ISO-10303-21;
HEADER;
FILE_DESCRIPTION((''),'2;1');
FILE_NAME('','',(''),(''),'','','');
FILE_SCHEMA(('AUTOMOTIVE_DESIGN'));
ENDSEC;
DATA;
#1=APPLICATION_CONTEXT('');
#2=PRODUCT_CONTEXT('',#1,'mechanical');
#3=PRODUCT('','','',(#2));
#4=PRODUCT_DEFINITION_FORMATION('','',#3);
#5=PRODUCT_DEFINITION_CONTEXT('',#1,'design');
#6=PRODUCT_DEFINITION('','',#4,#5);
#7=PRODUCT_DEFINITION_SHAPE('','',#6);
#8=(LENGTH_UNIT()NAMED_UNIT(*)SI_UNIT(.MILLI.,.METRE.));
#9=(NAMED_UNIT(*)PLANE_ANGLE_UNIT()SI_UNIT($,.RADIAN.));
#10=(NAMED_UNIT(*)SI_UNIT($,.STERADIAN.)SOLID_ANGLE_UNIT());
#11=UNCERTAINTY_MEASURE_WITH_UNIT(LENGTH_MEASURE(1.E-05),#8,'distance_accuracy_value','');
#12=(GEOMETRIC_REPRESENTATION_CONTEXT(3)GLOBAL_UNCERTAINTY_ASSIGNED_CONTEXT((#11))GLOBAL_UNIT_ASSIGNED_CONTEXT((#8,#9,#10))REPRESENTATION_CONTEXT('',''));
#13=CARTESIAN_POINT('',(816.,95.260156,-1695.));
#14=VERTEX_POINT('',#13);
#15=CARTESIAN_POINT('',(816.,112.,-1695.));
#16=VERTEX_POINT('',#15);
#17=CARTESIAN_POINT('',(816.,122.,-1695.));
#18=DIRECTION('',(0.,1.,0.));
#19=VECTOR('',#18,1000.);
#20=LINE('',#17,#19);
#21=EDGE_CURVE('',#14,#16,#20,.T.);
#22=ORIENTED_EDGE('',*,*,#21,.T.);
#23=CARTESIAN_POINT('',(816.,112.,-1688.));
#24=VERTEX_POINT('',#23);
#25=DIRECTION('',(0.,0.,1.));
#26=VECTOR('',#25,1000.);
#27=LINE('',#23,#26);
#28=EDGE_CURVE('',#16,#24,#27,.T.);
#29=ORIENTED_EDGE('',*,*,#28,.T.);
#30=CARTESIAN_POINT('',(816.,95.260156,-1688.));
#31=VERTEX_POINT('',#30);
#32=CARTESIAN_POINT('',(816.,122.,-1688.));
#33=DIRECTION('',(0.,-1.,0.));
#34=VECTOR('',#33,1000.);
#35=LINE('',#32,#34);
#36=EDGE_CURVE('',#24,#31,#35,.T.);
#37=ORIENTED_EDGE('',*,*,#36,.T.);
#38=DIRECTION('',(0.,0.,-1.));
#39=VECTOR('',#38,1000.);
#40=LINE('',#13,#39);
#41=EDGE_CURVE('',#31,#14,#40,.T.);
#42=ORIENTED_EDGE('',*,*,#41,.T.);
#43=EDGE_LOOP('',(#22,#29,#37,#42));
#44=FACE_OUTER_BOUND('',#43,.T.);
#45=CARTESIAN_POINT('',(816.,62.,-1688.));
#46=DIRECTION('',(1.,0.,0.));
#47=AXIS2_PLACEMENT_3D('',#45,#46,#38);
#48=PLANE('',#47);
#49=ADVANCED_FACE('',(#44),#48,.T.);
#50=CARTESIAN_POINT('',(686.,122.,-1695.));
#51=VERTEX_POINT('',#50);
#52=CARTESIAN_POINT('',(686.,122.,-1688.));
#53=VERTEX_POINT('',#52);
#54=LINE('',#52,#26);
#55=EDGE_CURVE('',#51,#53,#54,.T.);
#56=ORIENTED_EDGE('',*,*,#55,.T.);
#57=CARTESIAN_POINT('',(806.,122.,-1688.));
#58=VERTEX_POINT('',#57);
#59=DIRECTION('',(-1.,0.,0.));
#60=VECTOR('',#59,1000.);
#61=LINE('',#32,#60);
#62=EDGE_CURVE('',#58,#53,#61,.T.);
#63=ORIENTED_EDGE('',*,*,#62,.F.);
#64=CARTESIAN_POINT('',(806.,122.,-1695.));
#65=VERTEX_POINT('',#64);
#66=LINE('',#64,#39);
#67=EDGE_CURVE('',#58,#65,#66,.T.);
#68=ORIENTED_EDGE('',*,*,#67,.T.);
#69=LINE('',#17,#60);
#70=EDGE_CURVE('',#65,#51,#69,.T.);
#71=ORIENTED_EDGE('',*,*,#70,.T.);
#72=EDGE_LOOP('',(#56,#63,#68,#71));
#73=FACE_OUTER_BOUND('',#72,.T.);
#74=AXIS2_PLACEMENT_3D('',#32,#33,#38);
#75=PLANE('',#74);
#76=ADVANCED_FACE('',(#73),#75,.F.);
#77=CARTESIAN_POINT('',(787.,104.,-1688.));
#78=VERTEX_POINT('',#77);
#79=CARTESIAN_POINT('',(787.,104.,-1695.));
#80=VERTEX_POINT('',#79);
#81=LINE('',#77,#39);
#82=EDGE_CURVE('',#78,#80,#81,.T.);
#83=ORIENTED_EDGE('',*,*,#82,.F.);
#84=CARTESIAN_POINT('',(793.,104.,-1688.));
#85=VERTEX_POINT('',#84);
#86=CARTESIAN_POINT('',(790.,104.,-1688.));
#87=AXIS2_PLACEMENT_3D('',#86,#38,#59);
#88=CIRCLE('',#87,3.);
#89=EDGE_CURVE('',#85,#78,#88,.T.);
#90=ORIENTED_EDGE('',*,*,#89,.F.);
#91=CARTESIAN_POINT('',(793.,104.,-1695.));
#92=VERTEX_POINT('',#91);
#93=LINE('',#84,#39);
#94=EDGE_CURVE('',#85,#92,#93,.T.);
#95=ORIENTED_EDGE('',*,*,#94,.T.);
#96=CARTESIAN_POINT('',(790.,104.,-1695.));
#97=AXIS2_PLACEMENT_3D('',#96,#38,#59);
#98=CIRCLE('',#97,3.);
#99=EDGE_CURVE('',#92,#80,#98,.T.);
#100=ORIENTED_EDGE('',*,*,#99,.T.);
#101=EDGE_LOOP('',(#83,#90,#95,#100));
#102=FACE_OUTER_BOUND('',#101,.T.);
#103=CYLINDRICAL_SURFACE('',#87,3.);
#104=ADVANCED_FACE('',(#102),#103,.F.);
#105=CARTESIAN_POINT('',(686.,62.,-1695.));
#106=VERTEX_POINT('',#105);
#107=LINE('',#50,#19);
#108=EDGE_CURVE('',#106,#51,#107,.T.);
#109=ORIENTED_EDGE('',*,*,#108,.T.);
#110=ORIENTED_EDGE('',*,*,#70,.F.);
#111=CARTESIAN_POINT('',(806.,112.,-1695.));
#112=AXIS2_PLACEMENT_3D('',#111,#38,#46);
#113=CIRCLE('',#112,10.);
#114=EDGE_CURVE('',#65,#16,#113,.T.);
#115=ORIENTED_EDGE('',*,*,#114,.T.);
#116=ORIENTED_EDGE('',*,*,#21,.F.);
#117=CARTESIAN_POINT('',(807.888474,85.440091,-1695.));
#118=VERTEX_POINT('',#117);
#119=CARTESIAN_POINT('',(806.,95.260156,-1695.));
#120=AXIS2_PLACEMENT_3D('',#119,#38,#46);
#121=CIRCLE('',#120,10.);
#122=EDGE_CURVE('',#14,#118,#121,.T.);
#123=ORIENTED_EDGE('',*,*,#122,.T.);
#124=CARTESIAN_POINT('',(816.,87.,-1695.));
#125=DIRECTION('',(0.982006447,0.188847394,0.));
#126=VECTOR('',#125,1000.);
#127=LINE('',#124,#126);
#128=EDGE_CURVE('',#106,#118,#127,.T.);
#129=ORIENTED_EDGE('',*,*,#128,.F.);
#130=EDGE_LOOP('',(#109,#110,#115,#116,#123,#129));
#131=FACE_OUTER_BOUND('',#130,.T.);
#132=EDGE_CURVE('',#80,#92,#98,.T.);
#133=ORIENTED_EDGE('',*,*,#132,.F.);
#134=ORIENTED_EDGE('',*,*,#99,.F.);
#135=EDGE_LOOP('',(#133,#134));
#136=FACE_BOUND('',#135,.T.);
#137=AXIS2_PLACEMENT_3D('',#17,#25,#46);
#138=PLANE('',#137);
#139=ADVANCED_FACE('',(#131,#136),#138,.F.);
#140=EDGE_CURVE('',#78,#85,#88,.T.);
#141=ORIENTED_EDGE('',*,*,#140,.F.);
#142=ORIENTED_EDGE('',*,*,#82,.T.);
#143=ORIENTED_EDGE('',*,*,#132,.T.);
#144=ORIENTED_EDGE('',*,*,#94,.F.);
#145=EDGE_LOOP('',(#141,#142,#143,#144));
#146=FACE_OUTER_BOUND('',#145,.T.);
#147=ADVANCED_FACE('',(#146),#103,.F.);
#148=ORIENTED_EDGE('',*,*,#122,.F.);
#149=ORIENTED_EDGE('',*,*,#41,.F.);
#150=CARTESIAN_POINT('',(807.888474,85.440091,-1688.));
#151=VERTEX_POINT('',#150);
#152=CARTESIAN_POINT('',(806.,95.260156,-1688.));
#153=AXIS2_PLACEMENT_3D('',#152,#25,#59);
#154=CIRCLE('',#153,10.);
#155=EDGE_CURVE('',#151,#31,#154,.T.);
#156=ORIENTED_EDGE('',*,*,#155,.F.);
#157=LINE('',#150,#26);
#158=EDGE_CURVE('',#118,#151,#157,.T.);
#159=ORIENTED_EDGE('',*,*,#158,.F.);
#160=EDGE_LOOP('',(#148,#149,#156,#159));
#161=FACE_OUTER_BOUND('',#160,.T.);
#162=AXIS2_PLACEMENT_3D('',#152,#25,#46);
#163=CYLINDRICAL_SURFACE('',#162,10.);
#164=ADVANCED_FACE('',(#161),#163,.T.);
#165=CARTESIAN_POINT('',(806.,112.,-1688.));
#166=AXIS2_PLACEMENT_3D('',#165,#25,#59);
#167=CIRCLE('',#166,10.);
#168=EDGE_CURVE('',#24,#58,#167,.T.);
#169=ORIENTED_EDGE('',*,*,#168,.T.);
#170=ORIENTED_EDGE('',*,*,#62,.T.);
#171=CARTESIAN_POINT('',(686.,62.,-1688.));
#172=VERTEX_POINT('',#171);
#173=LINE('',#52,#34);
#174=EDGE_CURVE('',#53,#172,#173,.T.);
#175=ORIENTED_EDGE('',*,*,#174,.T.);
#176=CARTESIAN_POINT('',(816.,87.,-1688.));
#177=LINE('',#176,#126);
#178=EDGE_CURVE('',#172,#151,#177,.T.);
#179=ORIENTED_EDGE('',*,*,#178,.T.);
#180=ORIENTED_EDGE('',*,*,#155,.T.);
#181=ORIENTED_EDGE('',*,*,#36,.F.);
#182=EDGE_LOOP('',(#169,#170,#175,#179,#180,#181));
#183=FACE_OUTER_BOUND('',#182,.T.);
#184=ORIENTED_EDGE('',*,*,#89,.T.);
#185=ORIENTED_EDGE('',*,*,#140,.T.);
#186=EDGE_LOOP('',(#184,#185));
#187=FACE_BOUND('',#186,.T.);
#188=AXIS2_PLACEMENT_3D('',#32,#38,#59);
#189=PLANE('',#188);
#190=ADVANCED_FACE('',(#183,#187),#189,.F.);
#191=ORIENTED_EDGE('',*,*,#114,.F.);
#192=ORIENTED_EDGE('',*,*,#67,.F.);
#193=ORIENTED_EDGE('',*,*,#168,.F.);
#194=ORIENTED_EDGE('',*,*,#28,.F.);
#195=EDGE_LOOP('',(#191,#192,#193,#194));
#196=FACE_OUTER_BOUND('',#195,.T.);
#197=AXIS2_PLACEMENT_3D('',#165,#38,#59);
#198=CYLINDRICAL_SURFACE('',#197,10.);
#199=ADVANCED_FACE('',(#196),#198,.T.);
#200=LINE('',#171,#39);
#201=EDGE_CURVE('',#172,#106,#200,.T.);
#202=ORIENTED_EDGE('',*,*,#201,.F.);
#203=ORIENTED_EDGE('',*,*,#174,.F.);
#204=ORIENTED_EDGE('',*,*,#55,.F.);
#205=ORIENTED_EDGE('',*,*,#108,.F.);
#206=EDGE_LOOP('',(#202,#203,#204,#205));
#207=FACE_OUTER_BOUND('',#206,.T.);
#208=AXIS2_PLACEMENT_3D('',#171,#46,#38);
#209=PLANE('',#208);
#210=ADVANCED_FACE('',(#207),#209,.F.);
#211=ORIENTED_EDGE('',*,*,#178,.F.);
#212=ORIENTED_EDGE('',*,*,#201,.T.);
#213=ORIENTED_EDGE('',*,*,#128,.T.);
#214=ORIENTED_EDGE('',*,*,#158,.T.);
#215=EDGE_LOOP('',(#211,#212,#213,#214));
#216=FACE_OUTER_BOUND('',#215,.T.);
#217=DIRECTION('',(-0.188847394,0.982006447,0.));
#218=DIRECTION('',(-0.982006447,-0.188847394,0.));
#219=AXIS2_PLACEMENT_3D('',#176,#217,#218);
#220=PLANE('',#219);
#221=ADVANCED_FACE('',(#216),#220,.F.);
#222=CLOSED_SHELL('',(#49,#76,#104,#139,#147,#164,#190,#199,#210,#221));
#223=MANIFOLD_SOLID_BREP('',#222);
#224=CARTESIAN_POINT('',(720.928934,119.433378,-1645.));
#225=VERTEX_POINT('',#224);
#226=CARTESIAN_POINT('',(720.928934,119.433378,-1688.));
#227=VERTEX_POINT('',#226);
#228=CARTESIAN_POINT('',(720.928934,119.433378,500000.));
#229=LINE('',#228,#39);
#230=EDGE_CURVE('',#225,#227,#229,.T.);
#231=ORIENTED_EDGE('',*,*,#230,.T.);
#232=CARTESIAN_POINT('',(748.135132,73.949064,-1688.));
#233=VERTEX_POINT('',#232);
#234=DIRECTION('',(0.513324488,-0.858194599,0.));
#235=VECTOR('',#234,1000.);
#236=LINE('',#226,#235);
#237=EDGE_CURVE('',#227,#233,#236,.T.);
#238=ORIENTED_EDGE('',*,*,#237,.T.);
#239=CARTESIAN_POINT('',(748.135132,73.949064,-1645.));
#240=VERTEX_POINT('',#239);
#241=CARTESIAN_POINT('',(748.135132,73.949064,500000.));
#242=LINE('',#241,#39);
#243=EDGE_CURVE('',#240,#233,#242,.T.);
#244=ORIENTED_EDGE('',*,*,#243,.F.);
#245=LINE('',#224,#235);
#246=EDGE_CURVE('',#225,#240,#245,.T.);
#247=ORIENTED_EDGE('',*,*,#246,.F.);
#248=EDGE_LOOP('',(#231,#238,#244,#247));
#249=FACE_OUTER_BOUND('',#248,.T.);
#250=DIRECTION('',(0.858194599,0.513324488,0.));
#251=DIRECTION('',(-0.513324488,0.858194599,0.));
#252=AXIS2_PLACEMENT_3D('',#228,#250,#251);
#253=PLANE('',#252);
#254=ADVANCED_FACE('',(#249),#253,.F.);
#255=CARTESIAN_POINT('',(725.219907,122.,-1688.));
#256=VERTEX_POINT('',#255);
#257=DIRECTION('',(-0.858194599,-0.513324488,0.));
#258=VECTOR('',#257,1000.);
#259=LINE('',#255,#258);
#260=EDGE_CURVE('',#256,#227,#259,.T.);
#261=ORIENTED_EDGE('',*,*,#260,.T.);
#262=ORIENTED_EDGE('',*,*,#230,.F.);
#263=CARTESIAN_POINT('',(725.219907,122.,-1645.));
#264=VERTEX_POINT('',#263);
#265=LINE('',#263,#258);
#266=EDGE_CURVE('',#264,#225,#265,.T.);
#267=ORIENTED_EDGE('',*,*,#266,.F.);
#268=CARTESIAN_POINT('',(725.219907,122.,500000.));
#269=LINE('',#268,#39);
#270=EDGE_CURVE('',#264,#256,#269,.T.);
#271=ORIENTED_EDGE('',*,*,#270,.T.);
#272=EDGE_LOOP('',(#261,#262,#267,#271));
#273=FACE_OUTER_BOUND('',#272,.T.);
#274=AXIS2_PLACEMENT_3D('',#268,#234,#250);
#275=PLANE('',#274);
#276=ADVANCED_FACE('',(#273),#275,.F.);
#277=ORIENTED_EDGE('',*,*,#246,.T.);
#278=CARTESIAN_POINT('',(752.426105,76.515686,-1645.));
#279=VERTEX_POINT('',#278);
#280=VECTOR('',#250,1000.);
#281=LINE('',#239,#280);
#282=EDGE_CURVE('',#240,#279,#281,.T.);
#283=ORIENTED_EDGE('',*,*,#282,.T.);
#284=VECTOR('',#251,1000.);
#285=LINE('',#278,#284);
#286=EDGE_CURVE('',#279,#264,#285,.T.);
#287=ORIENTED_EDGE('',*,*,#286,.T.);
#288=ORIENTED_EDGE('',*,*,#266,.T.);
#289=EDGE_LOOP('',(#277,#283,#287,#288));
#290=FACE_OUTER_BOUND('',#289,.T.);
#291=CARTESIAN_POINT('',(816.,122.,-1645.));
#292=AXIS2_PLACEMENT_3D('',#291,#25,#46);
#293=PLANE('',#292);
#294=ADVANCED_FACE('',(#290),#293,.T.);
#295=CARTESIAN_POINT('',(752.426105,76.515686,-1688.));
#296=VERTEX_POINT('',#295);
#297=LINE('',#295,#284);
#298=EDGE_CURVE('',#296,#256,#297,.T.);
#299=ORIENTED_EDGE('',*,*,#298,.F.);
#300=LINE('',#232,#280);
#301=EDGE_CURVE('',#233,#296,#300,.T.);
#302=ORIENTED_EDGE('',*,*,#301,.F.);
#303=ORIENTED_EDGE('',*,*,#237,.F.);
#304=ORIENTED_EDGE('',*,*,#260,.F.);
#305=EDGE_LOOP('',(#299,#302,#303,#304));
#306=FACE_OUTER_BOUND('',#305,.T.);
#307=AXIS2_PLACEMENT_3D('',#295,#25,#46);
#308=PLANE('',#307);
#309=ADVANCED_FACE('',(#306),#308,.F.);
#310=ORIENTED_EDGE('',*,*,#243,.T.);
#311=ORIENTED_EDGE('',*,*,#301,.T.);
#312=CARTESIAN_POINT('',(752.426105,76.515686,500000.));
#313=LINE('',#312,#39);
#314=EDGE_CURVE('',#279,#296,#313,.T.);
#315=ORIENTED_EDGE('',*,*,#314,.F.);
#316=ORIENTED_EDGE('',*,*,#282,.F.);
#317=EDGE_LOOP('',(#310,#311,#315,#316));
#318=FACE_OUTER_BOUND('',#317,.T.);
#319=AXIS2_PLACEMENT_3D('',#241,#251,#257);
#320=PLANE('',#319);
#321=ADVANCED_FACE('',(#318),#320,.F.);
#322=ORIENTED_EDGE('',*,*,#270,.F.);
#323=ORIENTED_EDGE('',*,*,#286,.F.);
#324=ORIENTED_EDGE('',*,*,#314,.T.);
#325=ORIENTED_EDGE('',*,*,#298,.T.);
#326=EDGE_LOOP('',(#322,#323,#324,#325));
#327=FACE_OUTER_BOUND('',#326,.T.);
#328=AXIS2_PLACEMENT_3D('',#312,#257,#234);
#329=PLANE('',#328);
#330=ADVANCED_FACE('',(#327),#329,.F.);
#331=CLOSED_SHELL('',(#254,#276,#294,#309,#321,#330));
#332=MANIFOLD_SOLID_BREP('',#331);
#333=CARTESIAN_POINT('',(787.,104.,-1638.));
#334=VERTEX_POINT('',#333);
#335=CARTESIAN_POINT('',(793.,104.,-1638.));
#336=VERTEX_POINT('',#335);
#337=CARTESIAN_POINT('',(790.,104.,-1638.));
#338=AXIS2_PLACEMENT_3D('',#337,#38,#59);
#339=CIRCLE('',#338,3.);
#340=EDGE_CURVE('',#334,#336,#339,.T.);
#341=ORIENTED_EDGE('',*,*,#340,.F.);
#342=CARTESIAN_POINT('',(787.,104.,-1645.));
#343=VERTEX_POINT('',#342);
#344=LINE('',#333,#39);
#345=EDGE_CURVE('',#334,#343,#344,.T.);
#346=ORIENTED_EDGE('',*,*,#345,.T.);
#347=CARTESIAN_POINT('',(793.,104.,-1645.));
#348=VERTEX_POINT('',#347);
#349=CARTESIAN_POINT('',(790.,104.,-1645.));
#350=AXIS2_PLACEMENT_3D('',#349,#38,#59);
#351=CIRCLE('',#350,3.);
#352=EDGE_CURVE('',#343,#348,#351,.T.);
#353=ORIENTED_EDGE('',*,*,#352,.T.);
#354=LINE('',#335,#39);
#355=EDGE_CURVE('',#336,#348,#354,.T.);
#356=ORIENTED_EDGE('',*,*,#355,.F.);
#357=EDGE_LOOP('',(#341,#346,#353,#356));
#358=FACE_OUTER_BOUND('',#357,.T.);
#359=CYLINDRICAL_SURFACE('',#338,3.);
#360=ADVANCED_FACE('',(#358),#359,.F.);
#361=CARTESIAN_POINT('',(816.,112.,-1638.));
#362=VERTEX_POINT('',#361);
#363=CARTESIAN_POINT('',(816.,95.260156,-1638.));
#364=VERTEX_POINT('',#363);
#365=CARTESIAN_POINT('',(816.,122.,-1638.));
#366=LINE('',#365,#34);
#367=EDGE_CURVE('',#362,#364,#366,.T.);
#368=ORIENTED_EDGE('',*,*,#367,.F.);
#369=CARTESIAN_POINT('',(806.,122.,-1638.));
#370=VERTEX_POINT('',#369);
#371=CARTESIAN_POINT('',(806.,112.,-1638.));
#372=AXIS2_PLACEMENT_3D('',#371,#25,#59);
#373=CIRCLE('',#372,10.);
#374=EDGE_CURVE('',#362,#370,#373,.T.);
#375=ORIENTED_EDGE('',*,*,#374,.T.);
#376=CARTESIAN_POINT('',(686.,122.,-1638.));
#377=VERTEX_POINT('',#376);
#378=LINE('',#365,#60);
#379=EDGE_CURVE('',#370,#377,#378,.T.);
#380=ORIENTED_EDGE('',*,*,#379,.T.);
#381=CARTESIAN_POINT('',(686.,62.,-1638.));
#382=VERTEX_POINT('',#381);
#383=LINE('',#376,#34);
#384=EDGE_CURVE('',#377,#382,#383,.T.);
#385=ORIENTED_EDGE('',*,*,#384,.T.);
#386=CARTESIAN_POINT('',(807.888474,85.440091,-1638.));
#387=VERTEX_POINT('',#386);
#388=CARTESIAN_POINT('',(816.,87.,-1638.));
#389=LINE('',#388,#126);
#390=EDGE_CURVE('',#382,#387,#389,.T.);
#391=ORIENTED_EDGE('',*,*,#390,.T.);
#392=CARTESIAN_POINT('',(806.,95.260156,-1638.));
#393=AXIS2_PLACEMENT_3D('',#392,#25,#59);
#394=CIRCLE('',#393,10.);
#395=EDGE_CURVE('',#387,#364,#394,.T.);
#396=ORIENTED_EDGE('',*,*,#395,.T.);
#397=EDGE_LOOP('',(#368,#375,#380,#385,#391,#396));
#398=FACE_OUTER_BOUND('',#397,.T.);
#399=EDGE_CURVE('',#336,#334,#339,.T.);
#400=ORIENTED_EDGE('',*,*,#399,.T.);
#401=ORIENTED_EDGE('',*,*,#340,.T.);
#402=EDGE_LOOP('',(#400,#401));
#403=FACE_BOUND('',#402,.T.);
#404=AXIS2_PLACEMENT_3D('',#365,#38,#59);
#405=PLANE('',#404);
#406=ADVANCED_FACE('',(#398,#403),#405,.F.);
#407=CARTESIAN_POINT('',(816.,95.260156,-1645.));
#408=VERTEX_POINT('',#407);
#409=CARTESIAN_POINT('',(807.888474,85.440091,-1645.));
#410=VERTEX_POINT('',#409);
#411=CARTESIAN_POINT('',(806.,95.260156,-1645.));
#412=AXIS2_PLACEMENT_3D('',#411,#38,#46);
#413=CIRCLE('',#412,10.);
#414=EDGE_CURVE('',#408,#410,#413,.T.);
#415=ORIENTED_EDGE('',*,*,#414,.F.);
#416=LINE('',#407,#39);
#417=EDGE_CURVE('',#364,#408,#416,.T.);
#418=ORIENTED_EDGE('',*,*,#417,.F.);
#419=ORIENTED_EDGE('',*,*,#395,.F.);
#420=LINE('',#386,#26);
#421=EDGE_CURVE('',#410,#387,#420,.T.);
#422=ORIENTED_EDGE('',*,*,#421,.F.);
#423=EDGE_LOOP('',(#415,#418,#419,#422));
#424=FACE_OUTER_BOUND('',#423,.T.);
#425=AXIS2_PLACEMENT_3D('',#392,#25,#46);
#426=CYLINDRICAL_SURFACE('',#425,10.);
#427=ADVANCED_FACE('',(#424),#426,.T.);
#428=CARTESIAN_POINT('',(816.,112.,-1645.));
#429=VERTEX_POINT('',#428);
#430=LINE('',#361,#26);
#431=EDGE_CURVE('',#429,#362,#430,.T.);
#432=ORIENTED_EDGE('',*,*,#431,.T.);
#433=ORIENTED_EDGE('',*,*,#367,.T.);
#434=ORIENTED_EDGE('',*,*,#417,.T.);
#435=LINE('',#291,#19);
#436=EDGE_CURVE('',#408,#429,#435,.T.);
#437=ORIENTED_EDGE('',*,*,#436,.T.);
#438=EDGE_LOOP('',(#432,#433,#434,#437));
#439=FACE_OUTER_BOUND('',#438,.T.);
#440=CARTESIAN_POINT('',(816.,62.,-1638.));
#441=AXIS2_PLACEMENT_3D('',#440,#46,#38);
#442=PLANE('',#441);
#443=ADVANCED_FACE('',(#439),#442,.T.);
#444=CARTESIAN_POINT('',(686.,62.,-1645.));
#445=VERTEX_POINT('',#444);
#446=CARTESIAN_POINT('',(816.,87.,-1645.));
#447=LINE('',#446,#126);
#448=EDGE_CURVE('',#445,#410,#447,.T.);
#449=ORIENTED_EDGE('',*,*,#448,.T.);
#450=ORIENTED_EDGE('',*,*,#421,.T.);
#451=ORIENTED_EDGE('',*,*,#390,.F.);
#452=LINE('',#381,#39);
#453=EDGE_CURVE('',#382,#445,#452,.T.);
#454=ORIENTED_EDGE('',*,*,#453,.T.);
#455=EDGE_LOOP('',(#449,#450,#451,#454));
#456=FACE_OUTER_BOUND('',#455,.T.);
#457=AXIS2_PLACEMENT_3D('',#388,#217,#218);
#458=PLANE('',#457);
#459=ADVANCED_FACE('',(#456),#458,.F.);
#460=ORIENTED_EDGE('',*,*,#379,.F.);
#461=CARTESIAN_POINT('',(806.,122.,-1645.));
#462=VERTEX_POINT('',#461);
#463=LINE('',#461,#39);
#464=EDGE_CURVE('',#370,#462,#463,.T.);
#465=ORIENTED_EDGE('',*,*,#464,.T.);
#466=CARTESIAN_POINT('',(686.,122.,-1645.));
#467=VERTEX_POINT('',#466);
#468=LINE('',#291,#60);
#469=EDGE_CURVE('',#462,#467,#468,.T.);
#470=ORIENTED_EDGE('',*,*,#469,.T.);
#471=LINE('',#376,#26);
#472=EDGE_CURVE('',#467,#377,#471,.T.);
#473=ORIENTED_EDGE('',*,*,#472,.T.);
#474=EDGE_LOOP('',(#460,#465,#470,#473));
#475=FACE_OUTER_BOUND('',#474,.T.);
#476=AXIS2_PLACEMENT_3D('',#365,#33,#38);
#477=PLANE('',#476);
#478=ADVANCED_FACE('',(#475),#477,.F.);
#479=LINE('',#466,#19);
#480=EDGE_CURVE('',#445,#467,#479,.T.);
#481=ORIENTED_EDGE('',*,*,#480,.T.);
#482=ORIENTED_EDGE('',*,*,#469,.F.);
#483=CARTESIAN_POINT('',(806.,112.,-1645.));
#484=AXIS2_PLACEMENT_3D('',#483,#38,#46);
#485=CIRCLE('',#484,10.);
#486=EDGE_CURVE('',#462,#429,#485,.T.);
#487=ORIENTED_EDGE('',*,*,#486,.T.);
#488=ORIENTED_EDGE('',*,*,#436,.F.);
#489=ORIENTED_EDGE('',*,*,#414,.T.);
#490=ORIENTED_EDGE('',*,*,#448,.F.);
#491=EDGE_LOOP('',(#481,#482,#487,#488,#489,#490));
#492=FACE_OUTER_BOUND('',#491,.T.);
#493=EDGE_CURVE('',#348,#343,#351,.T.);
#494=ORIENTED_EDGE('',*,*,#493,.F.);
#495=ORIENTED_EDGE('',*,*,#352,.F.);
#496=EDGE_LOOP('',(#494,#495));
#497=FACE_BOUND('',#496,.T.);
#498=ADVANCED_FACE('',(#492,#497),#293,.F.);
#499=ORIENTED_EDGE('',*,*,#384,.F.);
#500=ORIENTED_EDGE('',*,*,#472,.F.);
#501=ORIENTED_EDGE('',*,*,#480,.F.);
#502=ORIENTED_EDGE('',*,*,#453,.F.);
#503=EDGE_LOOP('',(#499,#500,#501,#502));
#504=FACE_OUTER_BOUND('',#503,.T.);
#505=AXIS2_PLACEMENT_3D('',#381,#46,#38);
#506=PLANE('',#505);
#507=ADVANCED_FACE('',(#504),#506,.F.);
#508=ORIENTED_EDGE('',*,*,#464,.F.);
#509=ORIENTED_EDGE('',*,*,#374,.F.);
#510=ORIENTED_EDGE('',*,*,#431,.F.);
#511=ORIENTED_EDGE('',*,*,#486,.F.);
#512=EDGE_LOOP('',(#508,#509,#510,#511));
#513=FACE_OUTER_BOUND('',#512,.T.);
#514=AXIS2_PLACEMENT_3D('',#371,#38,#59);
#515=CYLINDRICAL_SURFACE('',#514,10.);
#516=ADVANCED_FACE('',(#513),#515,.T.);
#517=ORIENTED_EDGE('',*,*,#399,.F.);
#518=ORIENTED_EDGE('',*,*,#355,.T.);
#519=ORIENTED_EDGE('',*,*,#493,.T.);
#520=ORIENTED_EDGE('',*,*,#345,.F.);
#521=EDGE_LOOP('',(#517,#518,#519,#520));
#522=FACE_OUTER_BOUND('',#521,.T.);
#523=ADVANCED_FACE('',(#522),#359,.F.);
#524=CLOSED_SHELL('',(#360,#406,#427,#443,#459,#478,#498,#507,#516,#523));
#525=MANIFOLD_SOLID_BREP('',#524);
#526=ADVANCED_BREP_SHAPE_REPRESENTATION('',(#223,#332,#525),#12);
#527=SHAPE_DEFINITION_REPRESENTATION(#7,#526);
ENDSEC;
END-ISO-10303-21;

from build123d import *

# Parameters (mm, degrees)
SKETCH_1_W             = 7
SKETCH_1_H             = 60
EXTRUDE_1_DEPTH        = 130
SKETCH_2_R             = 3
CUT_EXTRUDE_1_DEPTH    = 826.099387953
FILLET_1_R             = 10
PATTERN_LINEAR_2_COUNT = 2
PATTERN_LINEAR_2_PITCH = 50
EXTRUDE_2_REACH        = 828.583


with BuildPart() as part:
    # 草图1 → 凸台-拉伸1 (new body)
    with BuildSketch(Plane(origin=(686, 0, 0), x_dir=(0, 0, -1), z_dir=(1, 0, 0))):
        with Locations((1691.5, 92)):
            Rectangle(SKETCH_1_W, SKETCH_1_H)
    extrude(amount=EXTRUDE_1_DEPTH)

    # 草图2 → 切除-拉伸1 (cut, through all)
    with BuildSketch(Plane(origin=(0, 0, -1695), x_dir=(-1, 0, 0), z_dir=(0, 0, -1))):
        with Locations((-790, 104)):
            Circle(SKETCH_2_R)
        Polygon((-816, 87), (-686, 62), (-816, 62), align=None)
    extrude(amount=-CUT_EXTRUDE_1_DEPTH, mode=Mode.SUBTRACT)

    # 圆角1
    fillet_1_edges = [part.edges().sort_by_distance(p)[0] for p in [
        (816, 122, -1691.5),
        (816, 87, -1691.5),
    ]]
    fillet(fillet_1_edges, radius=FILLET_1_R)


with BuildPart() as pattern_linear_2_1:
    # 阵列(线性)2: pattern copy
    add(part.part.moved(Location(Vector(0, 0, 1) * (1 * PATTERN_LINEAR_2_PITCH))))


with BuildPart() as body_3:

    # 草图3 → 凸台-拉伸2 (new, up to next)
    with BuildSketch(Plane.XY.offset(-1688), mode=Mode.PRIVATE) as extrude_2_sk1:
        Polygon((720.928933922, 119.43337756), (748.135131786, 73.949063805), (752.426104782, 76.515686245), (725.219906917, 122), align=None)
    extrude_2_tool1 = extrude(extrude_2_sk1.sketch, amount=EXTRUDE_2_REACH, mode=Mode.PRIVATE) - pattern_linear_2_1.part
    add(extrude_2_tool1.solids().sort_by_distance((736.677519, 97.974532, -1688))[0])


solid = Compound([part.part, pattern_linear_2_1.part, body_3.part])
